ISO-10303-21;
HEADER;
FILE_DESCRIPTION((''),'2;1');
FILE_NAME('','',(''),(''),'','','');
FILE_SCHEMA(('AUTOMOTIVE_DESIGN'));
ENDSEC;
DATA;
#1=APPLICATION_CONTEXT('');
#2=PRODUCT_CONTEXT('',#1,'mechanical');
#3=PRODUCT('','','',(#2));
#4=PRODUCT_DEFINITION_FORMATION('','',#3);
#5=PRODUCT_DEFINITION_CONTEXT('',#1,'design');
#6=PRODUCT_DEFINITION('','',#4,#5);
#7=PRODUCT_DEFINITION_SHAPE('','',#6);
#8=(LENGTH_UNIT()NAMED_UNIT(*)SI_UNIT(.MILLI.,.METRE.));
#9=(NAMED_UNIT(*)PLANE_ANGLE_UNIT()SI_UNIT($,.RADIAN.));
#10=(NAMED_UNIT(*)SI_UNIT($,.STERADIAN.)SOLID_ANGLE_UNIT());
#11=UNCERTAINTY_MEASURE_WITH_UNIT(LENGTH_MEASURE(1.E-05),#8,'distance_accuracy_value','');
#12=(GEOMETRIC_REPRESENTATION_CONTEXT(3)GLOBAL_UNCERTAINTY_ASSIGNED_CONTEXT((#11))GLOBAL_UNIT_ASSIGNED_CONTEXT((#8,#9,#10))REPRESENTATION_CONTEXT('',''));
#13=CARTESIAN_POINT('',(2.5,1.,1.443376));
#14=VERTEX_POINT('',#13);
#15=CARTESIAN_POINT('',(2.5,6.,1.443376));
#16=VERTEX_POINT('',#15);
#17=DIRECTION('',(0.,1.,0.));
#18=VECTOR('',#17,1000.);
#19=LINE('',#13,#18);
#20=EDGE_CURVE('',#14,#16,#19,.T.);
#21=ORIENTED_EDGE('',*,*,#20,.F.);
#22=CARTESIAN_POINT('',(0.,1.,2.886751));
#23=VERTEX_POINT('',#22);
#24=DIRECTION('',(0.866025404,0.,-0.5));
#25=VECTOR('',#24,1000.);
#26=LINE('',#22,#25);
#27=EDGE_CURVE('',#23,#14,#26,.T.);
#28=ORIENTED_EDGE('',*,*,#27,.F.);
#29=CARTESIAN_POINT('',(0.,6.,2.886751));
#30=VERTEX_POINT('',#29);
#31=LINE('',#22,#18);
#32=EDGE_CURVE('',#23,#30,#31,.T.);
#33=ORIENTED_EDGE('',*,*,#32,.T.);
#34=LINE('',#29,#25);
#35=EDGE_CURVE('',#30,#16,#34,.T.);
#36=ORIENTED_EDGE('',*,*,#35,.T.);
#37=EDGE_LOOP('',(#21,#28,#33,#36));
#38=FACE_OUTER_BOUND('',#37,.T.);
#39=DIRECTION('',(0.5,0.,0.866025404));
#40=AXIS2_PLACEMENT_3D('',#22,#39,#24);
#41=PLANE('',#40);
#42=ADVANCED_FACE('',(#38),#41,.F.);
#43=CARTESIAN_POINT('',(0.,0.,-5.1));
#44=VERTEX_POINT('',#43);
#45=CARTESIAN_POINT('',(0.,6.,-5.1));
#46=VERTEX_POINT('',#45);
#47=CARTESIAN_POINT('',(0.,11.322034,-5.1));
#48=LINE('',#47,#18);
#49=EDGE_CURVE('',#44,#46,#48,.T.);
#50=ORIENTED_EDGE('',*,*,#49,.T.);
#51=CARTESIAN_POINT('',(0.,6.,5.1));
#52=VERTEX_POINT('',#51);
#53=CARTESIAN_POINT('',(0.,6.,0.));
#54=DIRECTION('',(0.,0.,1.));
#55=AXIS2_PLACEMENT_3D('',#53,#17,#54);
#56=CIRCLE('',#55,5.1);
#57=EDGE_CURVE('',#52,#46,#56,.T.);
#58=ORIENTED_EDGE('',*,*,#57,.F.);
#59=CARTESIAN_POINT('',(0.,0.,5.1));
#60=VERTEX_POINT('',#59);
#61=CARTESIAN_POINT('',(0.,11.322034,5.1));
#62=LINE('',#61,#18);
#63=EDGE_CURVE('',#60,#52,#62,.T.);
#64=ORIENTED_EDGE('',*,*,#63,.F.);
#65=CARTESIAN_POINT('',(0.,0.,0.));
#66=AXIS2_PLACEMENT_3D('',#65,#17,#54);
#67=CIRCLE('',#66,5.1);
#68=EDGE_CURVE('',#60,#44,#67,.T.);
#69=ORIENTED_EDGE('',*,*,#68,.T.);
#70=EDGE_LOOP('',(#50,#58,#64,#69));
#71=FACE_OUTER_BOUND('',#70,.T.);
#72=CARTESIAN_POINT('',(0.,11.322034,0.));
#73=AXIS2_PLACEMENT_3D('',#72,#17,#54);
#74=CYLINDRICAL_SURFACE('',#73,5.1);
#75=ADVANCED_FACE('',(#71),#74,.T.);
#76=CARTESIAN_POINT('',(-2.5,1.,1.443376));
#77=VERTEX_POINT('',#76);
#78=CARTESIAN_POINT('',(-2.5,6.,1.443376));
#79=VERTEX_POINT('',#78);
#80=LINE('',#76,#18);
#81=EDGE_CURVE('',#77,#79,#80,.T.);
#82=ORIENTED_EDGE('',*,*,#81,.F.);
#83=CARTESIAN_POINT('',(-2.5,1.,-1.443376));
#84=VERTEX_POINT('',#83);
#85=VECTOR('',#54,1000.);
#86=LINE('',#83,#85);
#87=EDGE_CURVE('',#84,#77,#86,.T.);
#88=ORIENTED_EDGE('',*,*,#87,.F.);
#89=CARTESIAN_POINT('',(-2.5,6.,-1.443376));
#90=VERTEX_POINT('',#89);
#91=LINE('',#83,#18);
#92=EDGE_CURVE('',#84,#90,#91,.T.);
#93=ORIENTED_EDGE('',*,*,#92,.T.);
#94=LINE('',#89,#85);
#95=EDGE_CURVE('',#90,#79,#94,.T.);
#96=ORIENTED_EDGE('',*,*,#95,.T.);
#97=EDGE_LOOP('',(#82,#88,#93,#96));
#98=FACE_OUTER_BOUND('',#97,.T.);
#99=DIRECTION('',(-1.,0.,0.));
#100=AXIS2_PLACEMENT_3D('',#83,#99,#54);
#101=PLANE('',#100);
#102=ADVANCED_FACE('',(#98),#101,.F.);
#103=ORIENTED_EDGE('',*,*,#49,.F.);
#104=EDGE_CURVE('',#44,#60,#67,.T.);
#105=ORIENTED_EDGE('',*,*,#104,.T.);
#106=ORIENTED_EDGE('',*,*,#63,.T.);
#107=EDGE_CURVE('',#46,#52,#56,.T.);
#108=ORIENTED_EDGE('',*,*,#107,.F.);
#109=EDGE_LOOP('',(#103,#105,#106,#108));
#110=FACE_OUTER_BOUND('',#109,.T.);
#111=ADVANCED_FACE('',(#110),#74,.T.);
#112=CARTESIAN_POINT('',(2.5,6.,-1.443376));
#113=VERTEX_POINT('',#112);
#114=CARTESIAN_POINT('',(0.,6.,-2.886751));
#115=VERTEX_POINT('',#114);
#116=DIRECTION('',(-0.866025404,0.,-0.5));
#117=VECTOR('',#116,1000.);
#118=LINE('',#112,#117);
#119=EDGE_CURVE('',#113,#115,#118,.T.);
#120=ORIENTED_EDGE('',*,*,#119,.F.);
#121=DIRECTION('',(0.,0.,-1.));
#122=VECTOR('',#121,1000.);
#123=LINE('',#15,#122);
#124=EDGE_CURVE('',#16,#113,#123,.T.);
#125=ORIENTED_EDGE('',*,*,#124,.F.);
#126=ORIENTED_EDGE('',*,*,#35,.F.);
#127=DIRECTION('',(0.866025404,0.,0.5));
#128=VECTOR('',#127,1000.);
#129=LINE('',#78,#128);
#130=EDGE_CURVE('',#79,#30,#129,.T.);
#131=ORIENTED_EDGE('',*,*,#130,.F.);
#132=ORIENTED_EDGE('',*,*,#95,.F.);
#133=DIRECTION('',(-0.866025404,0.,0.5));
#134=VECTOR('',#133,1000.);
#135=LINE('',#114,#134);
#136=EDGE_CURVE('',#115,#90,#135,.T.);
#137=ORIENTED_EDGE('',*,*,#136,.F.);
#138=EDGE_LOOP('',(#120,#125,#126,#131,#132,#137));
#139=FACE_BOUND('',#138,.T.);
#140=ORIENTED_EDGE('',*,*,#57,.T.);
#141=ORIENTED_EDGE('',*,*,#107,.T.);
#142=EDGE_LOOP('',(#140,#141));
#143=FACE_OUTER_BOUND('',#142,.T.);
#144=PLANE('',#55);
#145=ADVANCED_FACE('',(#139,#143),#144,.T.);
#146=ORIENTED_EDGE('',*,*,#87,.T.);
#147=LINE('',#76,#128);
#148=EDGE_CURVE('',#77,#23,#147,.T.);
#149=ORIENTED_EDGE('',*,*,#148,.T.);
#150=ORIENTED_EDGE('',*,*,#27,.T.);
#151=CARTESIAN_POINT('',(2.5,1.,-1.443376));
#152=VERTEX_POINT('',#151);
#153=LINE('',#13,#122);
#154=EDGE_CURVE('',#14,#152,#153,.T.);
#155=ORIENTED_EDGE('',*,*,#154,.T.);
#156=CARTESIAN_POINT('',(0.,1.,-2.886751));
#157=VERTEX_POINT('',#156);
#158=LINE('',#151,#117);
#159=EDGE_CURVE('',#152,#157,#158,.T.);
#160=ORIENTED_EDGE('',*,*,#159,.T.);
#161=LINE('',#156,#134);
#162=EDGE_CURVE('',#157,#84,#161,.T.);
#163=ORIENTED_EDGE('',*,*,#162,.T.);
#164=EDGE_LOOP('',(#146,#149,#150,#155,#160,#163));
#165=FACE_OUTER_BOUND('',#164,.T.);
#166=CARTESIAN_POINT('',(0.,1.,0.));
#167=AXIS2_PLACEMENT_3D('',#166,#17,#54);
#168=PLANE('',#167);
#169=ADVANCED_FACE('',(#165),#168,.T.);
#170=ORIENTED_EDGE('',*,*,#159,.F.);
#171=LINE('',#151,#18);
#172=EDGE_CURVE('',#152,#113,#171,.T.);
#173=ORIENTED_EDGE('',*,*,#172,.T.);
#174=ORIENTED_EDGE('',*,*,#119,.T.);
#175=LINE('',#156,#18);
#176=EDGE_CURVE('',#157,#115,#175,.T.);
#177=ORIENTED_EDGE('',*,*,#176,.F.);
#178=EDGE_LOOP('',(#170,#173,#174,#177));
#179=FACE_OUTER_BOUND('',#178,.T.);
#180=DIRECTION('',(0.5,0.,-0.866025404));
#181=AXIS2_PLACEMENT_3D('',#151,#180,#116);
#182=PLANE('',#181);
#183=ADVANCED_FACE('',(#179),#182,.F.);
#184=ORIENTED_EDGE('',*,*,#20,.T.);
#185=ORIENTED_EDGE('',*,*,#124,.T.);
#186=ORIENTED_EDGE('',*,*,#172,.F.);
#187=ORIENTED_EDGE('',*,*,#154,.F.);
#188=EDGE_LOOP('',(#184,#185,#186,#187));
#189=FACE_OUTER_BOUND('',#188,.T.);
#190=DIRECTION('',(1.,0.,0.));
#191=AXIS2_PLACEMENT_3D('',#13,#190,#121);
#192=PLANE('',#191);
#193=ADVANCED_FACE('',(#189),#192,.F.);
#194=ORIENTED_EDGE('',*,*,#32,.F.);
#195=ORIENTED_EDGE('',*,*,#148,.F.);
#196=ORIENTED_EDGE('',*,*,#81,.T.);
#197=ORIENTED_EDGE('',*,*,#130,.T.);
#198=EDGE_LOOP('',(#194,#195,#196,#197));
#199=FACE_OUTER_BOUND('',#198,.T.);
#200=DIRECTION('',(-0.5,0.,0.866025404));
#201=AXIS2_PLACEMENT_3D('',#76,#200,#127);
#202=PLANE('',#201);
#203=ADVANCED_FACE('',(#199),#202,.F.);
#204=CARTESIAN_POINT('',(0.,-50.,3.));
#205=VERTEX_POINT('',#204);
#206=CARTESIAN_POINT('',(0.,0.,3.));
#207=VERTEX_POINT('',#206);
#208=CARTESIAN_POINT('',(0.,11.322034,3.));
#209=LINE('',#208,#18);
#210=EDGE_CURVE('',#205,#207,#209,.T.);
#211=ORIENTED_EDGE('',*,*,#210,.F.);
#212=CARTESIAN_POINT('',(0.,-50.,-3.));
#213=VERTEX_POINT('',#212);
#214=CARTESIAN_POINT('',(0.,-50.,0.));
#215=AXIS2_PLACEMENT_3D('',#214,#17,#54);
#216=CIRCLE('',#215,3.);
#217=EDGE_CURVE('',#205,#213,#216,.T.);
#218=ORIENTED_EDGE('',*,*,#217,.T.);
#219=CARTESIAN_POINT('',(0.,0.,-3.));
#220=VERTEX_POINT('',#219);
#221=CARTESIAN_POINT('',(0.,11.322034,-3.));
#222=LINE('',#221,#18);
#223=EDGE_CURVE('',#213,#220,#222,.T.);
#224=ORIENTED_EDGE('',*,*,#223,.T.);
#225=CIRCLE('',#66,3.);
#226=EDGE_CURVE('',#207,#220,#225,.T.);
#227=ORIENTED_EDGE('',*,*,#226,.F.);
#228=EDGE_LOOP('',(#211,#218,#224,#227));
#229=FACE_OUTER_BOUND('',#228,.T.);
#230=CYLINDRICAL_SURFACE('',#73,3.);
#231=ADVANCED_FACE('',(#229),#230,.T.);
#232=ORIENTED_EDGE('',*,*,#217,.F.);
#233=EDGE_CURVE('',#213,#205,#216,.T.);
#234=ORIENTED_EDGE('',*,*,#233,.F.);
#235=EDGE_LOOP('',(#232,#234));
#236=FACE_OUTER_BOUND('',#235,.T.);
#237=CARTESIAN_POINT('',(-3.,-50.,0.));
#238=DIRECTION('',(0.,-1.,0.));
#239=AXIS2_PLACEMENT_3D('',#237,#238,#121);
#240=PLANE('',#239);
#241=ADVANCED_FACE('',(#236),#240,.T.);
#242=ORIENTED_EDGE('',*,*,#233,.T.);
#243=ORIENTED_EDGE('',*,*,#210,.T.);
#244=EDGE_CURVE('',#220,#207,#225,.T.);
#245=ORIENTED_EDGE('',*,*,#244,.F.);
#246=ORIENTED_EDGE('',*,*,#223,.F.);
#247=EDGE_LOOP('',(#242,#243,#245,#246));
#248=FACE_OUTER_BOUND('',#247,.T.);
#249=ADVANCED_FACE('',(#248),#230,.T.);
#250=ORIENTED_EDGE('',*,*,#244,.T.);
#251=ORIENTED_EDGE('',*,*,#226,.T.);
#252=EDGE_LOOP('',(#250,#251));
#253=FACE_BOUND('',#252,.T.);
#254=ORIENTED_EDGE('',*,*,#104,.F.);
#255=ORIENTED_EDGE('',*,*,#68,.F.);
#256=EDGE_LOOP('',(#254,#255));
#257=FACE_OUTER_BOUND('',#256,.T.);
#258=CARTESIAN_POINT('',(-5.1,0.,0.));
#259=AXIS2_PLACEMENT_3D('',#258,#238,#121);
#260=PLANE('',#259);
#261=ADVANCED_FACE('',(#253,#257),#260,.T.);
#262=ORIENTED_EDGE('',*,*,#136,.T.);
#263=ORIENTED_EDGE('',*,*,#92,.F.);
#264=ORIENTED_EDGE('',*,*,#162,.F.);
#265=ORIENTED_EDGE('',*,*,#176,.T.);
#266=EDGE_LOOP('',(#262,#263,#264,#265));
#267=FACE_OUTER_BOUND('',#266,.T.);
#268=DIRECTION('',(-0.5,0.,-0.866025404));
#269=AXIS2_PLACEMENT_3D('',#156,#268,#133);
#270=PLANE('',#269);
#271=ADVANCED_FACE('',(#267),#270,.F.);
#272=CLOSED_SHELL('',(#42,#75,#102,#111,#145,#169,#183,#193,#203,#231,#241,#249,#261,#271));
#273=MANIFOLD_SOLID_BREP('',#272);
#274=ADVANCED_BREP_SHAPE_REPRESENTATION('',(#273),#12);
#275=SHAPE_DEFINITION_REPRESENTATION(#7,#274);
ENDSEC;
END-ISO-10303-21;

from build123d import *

# Parameters (mm, degrees)
CUT_EXTRUDE_1_DEPTH = 5


with BuildPart() as part:
    # Sketch 1 → Revolve 1 (revolve)
    with BuildSketch(Plane.XY, mode=Mode.PRIVATE) as revolve_1_sk:
        Polygon((0, 6), (-5.1, 6), (-5.1, 0), (-3, 0), (-3, -50), (0, -50), align=None)
    revolve(revolve_1_sk.sketch.rotate(Axis((0, 11.322033898, 0), (0, -1, 0)), 270), axis=Axis((0, 11.322033898, 0), (0, -1, 0)))

    # Sketch 2 → Cut-Extrude 1 (cut)
    with BuildSketch(Plane(origin=(0, 6, 0), x_dir=(1, 0, 0), z_dir=(0, 1, 0))):
        Polygon((0, 2.886751346), (-2.5, 1.443375673), (-2.5, -1.443375673), (0, -2.886751346), (2.5, -1.443375673), (2.5, 1.443375673), align=None)
    extrude(amount=-CUT_EXTRUDE_1_DEPTH, mode=Mode.SUBTRACT)


solid = part.part
